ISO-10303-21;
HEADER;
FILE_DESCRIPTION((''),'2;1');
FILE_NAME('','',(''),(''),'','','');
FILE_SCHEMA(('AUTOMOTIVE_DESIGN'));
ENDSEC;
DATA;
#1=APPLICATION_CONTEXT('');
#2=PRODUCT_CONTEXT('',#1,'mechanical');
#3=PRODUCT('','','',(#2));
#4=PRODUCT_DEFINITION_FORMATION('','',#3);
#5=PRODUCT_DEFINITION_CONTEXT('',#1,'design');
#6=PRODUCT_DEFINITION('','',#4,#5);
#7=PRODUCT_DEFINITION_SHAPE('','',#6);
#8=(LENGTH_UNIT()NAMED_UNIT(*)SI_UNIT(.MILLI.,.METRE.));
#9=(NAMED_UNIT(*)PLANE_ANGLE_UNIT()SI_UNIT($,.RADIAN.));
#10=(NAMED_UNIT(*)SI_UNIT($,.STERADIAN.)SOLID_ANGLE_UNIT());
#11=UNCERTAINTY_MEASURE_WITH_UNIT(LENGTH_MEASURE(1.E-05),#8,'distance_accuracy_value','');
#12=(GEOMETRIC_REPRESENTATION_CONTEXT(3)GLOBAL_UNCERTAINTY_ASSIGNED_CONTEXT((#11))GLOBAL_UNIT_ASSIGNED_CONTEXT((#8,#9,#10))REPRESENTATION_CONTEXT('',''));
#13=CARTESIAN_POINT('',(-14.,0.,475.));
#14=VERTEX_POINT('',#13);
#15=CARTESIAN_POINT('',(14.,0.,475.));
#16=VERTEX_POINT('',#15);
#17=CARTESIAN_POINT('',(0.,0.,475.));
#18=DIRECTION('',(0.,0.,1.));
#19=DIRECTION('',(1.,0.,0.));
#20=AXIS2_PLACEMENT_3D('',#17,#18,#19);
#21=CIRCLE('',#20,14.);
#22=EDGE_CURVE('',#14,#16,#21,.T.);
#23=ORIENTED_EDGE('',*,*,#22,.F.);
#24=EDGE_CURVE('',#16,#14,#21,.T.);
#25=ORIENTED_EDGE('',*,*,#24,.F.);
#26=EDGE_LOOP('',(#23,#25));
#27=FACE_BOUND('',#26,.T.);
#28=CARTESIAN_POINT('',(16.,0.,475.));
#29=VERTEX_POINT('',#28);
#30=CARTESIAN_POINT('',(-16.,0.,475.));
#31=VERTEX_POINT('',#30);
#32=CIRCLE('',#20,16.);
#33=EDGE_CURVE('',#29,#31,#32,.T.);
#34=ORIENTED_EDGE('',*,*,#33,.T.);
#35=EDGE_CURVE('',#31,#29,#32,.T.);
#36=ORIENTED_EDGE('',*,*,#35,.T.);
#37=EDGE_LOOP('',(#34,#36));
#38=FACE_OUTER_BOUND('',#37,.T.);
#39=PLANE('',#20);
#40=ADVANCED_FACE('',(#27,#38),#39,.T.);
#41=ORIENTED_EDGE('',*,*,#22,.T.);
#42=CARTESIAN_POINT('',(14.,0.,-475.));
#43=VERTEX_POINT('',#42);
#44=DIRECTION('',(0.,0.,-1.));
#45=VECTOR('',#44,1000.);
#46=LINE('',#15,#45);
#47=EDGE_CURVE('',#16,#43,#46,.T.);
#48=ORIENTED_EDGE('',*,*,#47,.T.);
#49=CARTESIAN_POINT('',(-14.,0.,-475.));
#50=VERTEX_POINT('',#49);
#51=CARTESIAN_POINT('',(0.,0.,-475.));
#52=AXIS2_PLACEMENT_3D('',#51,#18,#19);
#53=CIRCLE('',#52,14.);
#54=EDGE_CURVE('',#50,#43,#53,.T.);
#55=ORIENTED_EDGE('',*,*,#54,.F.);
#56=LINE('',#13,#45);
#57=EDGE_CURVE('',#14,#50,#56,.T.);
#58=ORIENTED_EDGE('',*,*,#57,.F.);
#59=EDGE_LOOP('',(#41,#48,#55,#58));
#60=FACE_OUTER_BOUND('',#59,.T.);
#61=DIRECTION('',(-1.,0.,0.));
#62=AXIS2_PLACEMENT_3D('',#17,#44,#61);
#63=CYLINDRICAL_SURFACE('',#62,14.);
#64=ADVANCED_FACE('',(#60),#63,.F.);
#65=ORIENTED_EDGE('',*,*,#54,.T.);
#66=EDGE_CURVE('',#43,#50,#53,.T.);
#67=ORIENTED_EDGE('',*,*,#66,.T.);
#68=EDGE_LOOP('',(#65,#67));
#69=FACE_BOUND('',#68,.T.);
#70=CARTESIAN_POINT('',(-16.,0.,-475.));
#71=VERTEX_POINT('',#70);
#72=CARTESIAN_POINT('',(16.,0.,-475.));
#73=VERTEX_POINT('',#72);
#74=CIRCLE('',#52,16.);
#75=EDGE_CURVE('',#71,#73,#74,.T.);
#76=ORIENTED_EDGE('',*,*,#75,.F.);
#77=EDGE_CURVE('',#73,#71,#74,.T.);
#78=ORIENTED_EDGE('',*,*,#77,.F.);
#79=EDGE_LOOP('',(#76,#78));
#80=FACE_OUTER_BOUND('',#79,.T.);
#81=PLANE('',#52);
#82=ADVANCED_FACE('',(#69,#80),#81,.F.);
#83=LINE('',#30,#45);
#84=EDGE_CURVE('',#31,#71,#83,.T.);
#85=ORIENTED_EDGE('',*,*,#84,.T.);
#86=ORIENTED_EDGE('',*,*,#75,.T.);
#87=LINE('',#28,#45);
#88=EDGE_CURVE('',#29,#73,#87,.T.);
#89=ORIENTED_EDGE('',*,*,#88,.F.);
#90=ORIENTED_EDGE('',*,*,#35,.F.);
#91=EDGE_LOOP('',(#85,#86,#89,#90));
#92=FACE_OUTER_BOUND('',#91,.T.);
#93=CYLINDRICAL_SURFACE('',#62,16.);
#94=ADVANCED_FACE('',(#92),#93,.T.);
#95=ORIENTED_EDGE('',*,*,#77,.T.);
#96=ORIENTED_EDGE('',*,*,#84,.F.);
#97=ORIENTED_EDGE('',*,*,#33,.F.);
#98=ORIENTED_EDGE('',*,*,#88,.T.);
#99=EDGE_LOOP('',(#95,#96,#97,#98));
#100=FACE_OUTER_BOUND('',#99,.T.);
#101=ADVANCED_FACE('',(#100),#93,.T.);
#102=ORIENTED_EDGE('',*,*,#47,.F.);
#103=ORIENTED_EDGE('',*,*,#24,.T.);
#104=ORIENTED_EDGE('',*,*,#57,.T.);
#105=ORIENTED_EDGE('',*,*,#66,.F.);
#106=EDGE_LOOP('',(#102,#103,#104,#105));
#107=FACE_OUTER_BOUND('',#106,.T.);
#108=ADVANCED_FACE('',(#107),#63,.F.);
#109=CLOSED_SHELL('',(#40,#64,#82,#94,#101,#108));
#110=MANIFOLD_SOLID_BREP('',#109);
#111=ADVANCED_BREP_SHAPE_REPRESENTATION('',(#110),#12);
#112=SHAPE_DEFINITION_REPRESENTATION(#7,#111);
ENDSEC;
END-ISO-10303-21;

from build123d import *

# Parameters (mm, degrees)
SKETCH_1_R      = 16
SKETCH_1_R_2    = 14
EXTRUDE_1_DEPTH = 475


with BuildPart() as part:
    # 草图1 → 凸台-拉伸1 (new, symmetric)
    with BuildSketch(Plane.XY):
        with Locations(Location((0, 0, 0), (0, 0, 180))):
            Circle(SKETCH_1_R)
        with Locations(Location((0, 0, 0), (0, 0, 180))):
            Circle(SKETCH_1_R_2, mode=Mode.SUBTRACT)
    extrude(amount=EXTRUDE_1_DEPTH, both=True)


solid = part.part
